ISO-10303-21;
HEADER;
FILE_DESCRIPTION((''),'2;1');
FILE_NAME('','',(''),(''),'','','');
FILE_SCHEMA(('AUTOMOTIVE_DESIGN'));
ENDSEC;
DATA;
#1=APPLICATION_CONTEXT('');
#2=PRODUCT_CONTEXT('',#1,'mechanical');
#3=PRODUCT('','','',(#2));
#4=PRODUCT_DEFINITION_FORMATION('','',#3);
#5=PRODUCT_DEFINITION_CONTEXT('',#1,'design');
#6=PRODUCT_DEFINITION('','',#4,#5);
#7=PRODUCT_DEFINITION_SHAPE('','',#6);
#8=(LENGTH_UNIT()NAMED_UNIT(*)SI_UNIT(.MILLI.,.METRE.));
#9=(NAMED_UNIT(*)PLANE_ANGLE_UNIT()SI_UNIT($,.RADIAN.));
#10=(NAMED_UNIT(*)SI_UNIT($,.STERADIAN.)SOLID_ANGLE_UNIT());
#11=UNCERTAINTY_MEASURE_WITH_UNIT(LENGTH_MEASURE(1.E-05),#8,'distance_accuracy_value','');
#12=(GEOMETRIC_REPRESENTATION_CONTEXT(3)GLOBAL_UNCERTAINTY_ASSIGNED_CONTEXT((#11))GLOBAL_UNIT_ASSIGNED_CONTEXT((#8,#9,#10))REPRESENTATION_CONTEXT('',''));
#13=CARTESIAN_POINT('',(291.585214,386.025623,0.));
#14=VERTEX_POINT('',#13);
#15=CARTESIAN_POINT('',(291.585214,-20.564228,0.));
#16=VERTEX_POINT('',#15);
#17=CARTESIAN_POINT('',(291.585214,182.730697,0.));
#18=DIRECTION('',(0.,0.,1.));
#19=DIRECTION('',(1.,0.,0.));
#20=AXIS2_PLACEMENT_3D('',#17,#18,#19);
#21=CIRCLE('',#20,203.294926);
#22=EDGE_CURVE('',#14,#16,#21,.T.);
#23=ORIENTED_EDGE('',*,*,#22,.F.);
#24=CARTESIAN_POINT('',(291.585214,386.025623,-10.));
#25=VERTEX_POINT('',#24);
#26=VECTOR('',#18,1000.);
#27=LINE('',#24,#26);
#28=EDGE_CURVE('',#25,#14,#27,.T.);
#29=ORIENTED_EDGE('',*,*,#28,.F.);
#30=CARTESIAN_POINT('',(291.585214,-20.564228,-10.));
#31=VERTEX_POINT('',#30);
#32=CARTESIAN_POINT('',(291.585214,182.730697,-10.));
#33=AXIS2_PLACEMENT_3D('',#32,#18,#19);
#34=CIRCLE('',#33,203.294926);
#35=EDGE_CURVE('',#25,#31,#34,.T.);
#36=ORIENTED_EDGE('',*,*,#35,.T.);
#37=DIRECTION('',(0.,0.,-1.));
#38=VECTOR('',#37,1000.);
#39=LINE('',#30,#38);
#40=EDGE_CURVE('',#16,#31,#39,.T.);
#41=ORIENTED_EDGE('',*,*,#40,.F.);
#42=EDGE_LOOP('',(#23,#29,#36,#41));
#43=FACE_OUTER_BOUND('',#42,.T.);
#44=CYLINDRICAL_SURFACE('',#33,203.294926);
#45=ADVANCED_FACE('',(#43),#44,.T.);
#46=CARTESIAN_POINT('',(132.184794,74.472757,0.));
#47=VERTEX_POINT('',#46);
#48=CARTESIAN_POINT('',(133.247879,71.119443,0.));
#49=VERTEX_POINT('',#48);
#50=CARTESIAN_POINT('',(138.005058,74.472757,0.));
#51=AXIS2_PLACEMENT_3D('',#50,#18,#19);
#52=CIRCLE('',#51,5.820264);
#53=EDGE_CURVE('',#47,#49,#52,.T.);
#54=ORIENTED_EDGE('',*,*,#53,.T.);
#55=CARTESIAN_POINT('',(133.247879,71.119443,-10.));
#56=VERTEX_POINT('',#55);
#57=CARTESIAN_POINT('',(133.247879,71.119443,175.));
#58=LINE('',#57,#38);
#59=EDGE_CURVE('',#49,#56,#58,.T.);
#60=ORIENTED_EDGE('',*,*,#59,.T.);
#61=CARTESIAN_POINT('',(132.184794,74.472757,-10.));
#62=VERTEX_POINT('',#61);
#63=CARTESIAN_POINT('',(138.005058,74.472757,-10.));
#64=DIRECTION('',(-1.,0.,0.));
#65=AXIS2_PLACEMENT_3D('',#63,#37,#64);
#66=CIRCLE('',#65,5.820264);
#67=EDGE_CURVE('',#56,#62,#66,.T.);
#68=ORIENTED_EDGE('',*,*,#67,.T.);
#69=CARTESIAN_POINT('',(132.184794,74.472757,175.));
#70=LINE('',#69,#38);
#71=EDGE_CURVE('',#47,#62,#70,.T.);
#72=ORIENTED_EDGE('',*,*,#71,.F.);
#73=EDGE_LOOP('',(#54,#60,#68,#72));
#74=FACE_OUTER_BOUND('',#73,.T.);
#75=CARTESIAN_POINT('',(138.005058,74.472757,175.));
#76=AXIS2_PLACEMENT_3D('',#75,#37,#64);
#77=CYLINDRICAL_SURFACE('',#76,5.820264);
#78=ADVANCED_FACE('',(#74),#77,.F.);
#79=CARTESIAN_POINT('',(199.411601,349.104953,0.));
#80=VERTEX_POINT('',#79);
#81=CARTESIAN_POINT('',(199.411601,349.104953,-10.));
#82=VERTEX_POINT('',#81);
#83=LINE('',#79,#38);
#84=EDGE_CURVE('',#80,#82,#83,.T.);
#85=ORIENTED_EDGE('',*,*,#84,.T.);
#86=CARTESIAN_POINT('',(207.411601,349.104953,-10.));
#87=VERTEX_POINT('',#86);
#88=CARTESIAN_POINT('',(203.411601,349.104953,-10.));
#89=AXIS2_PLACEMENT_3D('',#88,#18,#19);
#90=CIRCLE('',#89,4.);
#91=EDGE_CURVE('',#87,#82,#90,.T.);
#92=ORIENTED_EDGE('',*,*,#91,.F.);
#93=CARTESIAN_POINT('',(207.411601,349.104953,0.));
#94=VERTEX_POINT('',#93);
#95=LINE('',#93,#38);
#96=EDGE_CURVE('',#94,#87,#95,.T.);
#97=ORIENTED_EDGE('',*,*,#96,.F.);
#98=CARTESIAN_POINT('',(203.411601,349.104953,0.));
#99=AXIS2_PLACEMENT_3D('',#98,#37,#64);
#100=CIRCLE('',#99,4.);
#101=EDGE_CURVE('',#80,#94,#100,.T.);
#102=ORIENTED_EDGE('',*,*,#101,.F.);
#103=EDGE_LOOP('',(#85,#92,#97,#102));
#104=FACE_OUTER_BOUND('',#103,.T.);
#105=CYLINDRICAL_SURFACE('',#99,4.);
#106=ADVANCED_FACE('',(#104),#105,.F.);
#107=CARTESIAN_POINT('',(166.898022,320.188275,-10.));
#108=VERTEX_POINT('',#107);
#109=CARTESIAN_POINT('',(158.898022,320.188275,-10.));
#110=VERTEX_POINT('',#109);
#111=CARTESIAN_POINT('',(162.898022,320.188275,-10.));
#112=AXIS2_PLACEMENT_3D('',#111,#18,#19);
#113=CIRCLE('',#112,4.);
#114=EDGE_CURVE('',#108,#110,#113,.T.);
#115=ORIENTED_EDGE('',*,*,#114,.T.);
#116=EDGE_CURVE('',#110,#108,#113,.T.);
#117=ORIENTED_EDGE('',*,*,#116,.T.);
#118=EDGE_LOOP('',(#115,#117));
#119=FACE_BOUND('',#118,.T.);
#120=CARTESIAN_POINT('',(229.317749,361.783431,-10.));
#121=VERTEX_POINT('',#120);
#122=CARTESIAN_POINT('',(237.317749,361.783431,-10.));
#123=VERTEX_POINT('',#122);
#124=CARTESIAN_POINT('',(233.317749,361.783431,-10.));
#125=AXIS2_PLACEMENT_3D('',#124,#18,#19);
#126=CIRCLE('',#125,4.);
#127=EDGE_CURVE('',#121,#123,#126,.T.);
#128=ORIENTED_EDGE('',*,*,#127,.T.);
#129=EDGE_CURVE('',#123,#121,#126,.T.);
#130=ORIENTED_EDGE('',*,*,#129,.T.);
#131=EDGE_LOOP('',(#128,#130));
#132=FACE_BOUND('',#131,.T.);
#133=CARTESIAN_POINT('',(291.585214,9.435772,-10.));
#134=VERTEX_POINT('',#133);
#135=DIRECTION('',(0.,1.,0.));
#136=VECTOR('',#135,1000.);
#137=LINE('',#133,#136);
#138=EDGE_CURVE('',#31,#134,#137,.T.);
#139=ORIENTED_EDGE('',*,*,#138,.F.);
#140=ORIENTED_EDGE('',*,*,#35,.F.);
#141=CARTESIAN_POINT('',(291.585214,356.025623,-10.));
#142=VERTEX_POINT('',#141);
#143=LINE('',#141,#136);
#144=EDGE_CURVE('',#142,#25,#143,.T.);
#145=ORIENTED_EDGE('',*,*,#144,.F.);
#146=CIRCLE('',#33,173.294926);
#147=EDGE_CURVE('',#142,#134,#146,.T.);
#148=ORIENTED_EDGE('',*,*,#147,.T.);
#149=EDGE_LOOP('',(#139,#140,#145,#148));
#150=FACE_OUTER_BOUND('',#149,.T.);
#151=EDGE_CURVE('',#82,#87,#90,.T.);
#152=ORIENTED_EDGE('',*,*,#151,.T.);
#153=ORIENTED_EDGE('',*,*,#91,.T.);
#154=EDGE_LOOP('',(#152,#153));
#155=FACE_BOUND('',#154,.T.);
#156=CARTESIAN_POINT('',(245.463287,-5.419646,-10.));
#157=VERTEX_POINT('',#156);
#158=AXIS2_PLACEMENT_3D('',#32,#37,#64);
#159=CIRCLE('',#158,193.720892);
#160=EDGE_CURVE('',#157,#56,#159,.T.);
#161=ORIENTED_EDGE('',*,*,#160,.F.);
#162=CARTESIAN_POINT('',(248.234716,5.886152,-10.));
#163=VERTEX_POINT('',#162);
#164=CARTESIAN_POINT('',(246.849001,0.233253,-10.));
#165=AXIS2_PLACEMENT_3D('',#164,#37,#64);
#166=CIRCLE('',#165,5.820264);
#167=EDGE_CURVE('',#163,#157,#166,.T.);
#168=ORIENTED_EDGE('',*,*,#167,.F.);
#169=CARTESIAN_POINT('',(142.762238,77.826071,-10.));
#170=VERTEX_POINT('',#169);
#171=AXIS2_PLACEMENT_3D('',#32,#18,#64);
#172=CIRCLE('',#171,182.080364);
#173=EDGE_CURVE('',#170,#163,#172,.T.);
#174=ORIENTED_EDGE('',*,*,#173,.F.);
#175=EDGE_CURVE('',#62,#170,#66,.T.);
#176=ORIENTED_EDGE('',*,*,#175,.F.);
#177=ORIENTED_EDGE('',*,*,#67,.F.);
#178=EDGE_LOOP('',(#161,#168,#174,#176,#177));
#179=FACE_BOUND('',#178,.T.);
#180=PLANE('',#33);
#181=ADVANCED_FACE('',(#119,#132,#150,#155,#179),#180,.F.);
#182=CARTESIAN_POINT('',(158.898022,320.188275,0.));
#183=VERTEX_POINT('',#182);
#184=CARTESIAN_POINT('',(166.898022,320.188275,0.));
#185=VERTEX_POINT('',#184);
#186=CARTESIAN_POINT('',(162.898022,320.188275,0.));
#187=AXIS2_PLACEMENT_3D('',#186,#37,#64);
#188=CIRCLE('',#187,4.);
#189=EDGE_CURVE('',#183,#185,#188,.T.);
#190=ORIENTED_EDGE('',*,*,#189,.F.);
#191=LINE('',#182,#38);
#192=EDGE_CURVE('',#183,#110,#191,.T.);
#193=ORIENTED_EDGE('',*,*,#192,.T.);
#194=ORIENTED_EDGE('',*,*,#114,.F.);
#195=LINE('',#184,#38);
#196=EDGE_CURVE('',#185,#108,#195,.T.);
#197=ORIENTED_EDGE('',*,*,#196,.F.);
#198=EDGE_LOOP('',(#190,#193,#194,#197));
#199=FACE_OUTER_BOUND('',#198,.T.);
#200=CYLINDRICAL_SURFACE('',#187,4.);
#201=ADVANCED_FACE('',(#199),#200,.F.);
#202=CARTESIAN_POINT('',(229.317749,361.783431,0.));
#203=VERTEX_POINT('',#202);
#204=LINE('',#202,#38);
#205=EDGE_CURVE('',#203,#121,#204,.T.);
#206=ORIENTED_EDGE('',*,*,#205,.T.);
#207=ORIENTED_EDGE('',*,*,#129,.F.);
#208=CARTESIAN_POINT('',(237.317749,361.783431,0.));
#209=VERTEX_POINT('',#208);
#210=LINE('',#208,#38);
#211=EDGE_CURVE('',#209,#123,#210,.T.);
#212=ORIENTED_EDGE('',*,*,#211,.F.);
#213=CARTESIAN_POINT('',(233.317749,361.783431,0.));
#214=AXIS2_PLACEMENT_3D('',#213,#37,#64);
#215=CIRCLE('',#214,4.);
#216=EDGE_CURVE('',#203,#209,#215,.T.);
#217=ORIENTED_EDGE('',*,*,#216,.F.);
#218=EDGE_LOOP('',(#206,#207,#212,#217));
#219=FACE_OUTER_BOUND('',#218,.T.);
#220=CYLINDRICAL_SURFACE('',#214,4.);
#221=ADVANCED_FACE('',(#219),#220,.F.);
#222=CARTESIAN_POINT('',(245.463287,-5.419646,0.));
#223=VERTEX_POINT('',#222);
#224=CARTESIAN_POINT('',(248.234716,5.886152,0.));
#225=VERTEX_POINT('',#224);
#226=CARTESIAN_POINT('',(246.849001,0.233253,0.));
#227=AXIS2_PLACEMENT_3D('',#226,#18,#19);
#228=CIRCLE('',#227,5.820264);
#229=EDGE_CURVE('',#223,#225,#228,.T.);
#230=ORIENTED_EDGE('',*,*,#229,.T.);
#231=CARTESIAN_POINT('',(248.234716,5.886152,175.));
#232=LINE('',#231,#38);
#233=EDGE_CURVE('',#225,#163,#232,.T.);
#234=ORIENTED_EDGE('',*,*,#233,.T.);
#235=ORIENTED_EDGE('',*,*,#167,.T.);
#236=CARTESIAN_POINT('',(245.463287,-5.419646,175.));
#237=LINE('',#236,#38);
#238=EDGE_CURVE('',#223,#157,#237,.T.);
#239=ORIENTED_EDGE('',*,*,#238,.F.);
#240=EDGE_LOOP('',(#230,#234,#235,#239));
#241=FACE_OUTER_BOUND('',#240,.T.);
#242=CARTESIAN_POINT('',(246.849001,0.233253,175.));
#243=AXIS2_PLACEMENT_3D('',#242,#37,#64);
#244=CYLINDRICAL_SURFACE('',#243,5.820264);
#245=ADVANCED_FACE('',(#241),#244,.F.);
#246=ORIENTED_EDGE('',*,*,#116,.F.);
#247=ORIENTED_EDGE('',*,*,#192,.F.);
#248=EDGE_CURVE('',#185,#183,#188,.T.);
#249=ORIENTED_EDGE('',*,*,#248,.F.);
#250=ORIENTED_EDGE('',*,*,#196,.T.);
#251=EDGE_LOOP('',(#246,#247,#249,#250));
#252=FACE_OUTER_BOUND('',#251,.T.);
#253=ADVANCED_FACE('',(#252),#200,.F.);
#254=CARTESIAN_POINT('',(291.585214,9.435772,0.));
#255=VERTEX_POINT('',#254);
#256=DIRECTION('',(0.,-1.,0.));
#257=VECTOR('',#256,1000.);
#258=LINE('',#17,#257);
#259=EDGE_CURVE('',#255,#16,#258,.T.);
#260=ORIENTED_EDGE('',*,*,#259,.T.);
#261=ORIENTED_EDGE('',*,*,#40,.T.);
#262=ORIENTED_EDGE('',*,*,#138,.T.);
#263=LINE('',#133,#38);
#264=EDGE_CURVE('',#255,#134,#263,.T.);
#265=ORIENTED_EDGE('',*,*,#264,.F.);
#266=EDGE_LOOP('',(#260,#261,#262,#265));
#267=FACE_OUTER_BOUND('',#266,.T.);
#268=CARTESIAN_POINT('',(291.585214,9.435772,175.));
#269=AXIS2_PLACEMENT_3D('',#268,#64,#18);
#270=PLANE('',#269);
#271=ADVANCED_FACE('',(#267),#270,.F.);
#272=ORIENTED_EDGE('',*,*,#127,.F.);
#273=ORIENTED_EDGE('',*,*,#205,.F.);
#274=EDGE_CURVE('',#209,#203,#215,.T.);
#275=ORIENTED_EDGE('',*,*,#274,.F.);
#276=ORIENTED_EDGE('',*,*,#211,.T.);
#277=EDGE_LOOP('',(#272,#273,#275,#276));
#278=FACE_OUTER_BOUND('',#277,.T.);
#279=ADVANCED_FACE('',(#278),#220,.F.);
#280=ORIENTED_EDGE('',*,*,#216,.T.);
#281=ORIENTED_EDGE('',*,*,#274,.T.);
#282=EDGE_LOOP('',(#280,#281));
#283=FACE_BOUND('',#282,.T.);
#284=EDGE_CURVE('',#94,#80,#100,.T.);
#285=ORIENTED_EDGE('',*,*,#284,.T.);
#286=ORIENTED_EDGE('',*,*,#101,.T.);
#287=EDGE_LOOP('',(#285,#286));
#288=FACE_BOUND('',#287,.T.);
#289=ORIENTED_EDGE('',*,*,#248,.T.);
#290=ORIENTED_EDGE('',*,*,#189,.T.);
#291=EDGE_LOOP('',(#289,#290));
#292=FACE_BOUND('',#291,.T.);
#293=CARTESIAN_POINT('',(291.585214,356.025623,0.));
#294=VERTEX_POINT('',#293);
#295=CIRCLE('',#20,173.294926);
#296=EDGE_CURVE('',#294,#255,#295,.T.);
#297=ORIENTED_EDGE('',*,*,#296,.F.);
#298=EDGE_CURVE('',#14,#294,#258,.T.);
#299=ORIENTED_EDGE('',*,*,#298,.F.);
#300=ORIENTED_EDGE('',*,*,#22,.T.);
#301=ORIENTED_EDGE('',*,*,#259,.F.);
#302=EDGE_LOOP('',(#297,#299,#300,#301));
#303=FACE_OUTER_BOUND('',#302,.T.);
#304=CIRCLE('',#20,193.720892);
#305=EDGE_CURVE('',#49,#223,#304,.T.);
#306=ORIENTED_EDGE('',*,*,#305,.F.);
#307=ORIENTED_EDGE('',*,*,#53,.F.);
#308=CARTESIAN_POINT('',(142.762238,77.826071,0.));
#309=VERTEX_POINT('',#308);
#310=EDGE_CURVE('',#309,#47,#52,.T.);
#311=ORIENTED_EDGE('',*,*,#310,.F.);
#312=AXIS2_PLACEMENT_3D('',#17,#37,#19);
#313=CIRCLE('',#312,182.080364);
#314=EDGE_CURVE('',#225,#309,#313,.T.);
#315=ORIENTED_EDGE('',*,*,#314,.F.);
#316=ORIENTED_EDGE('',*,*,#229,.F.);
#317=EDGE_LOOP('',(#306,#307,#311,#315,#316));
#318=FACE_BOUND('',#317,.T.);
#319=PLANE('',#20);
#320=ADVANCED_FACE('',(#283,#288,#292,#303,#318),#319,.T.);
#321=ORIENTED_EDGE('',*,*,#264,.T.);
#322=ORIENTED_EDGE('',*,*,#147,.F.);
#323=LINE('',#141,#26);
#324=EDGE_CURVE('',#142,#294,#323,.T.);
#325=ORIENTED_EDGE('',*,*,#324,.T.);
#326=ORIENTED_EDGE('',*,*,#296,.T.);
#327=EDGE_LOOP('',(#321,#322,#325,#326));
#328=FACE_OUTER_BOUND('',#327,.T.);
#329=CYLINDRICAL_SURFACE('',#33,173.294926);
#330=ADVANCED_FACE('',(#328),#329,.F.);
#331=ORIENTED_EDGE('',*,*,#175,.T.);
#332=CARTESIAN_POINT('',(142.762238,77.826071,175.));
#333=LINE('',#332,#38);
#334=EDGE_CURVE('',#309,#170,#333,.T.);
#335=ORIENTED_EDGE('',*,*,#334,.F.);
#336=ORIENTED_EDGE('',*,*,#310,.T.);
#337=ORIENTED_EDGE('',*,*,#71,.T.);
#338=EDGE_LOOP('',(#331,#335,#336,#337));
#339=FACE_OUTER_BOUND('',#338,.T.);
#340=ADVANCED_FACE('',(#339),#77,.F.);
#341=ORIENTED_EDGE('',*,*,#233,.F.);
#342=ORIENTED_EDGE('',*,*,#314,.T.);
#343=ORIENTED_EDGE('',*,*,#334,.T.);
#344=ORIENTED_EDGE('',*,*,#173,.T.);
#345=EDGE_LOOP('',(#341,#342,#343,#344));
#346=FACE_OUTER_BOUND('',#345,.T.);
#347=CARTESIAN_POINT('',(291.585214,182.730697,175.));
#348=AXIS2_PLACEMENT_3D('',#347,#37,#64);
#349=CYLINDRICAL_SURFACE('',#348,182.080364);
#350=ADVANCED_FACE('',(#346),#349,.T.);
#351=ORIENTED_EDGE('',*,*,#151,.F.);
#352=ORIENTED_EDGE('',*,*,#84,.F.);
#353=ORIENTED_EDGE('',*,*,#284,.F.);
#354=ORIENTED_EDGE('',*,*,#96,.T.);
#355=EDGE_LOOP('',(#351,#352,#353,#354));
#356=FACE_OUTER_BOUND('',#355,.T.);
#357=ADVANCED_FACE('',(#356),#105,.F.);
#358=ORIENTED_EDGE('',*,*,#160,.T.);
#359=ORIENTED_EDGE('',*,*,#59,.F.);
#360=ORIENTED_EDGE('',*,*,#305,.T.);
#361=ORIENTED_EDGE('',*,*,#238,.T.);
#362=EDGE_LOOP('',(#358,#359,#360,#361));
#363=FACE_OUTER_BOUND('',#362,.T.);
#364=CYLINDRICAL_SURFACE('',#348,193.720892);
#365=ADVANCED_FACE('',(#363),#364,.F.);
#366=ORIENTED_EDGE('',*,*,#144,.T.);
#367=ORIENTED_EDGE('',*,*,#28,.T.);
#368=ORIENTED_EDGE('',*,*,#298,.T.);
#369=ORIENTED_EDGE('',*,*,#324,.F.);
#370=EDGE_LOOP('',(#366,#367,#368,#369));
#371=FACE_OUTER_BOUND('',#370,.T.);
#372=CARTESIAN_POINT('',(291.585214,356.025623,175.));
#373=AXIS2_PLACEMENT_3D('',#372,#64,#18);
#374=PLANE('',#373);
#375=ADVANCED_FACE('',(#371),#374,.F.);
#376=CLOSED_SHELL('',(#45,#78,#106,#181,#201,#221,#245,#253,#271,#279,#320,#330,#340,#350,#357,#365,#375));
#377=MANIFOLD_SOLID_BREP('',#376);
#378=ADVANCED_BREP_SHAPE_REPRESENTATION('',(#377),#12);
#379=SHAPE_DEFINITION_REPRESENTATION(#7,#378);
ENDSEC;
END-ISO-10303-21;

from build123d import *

# Parameters (mm, degrees)
SKETCH1_R               = 203.294925519
SKETCH1_R_2             = 173.294925519
BOSS_EXTRUDE1_DEPTH     = 10
CUT_EXTRUDE1_START      = -185
CUT_EXTRUDE1_DEPTH      = 185
CUT_EXTRUDE2_DEPTH      = 185
CUT_EXTRUDE3_DEPTH      = 484.877792972
CUT_EXTRUDE3_DEPTH_BACK = 484.877792972
SKETCH4_R               = 4


with BuildPart() as part:
    # Sketch1 → Boss-Extrude1 (new body)
    with BuildSketch(Plane.XY):
        with Locations((291.585214163, 182.730697222)):
            Circle(SKETCH1_R)
        with Locations((291.585214163, 182.730697222)):
            Circle(SKETCH1_R_2, mode=Mode.SUBTRACT)
    extrude(amount=-BOSS_EXTRUDE1_DEPTH)

    # Sketch2 → Cut-Extrude1 (cut)
    with BuildSketch(Plane(origin=(0, 0, -10), x_dir=(-1, 0, 0), z_dir=(0, 0, -1)).offset(CUT_EXTRUDE1_START)):
        with BuildLine():
            Line((-291.585214163, 9.435771703), (-291.585214163, -33.905509081))
            ThreePointArc((-291.585214163, -33.905509081), (-508.221420466, 182.730697222), (-291.585214163, 399.366903525))
            Line((-291.585214163, 399.366903525), (-291.585214163, 356.025622742))
            ThreePointArc((-291.585214163, 356.025622742), (-464.880139683, 182.730697222), (-291.585214163, 9.435771703))
        make_face()
    extrude(amount=CUT_EXTRUDE1_DEPTH, mode=Mode.SUBTRACT)

    # Sketch3 → Cut-Extrude2 (cut)
    with BuildSketch(Plane(origin=(0, 0, -10), x_dir=(-1, 0, 0), z_dir=(0, 0, -1))):
        with BuildLine():
            ThreePointArc((-245.463287057, -5.419646314), (-182.427275621, 22.692175653), (-133.247878722, 71.11944269))
            ThreePointArc((-133.247878722, 71.11944269), (-134.651744503, 79.229936459), (-142.762238272, 77.826070678))
            ThreePointArc((-142.762238272, 77.826070678), (-188.98648588, 32.30875807), (-248.234715516, 5.886152238))
            ThreePointArc((-248.234715516, 5.886152238), (-252.501900562, -1.152461267), (-245.463287057, -5.419646314))
        make_face()
    extrude(amount=-CUT_EXTRUDE2_DEPTH, mode=Mode.SUBTRACT)

    # Sketch4 → Cut-Extrude3 (cut, two sides: drawn at the far end of the back side and taken through both)
    with BuildSketch(Plane(origin=(0, 0, -10), x_dir=(-1, 0, 0), z_dir=(0, 0, -1)).offset(-CUT_EXTRUDE3_DEPTH_BACK)):
        with Locations((-203.411601384, 349.104953001)):
            Circle(SKETCH4_R)
        with Locations((-233.317748738, 361.783430933)):
            Circle(SKETCH4_R)
        with Locations((-162.898022452, 320.188274917)):
            Circle(SKETCH4_R)
    extrude(amount=CUT_EXTRUDE3_DEPTH + CUT_EXTRUDE3_DEPTH_BACK, mode=Mode.SUBTRACT)


solid = part.part
